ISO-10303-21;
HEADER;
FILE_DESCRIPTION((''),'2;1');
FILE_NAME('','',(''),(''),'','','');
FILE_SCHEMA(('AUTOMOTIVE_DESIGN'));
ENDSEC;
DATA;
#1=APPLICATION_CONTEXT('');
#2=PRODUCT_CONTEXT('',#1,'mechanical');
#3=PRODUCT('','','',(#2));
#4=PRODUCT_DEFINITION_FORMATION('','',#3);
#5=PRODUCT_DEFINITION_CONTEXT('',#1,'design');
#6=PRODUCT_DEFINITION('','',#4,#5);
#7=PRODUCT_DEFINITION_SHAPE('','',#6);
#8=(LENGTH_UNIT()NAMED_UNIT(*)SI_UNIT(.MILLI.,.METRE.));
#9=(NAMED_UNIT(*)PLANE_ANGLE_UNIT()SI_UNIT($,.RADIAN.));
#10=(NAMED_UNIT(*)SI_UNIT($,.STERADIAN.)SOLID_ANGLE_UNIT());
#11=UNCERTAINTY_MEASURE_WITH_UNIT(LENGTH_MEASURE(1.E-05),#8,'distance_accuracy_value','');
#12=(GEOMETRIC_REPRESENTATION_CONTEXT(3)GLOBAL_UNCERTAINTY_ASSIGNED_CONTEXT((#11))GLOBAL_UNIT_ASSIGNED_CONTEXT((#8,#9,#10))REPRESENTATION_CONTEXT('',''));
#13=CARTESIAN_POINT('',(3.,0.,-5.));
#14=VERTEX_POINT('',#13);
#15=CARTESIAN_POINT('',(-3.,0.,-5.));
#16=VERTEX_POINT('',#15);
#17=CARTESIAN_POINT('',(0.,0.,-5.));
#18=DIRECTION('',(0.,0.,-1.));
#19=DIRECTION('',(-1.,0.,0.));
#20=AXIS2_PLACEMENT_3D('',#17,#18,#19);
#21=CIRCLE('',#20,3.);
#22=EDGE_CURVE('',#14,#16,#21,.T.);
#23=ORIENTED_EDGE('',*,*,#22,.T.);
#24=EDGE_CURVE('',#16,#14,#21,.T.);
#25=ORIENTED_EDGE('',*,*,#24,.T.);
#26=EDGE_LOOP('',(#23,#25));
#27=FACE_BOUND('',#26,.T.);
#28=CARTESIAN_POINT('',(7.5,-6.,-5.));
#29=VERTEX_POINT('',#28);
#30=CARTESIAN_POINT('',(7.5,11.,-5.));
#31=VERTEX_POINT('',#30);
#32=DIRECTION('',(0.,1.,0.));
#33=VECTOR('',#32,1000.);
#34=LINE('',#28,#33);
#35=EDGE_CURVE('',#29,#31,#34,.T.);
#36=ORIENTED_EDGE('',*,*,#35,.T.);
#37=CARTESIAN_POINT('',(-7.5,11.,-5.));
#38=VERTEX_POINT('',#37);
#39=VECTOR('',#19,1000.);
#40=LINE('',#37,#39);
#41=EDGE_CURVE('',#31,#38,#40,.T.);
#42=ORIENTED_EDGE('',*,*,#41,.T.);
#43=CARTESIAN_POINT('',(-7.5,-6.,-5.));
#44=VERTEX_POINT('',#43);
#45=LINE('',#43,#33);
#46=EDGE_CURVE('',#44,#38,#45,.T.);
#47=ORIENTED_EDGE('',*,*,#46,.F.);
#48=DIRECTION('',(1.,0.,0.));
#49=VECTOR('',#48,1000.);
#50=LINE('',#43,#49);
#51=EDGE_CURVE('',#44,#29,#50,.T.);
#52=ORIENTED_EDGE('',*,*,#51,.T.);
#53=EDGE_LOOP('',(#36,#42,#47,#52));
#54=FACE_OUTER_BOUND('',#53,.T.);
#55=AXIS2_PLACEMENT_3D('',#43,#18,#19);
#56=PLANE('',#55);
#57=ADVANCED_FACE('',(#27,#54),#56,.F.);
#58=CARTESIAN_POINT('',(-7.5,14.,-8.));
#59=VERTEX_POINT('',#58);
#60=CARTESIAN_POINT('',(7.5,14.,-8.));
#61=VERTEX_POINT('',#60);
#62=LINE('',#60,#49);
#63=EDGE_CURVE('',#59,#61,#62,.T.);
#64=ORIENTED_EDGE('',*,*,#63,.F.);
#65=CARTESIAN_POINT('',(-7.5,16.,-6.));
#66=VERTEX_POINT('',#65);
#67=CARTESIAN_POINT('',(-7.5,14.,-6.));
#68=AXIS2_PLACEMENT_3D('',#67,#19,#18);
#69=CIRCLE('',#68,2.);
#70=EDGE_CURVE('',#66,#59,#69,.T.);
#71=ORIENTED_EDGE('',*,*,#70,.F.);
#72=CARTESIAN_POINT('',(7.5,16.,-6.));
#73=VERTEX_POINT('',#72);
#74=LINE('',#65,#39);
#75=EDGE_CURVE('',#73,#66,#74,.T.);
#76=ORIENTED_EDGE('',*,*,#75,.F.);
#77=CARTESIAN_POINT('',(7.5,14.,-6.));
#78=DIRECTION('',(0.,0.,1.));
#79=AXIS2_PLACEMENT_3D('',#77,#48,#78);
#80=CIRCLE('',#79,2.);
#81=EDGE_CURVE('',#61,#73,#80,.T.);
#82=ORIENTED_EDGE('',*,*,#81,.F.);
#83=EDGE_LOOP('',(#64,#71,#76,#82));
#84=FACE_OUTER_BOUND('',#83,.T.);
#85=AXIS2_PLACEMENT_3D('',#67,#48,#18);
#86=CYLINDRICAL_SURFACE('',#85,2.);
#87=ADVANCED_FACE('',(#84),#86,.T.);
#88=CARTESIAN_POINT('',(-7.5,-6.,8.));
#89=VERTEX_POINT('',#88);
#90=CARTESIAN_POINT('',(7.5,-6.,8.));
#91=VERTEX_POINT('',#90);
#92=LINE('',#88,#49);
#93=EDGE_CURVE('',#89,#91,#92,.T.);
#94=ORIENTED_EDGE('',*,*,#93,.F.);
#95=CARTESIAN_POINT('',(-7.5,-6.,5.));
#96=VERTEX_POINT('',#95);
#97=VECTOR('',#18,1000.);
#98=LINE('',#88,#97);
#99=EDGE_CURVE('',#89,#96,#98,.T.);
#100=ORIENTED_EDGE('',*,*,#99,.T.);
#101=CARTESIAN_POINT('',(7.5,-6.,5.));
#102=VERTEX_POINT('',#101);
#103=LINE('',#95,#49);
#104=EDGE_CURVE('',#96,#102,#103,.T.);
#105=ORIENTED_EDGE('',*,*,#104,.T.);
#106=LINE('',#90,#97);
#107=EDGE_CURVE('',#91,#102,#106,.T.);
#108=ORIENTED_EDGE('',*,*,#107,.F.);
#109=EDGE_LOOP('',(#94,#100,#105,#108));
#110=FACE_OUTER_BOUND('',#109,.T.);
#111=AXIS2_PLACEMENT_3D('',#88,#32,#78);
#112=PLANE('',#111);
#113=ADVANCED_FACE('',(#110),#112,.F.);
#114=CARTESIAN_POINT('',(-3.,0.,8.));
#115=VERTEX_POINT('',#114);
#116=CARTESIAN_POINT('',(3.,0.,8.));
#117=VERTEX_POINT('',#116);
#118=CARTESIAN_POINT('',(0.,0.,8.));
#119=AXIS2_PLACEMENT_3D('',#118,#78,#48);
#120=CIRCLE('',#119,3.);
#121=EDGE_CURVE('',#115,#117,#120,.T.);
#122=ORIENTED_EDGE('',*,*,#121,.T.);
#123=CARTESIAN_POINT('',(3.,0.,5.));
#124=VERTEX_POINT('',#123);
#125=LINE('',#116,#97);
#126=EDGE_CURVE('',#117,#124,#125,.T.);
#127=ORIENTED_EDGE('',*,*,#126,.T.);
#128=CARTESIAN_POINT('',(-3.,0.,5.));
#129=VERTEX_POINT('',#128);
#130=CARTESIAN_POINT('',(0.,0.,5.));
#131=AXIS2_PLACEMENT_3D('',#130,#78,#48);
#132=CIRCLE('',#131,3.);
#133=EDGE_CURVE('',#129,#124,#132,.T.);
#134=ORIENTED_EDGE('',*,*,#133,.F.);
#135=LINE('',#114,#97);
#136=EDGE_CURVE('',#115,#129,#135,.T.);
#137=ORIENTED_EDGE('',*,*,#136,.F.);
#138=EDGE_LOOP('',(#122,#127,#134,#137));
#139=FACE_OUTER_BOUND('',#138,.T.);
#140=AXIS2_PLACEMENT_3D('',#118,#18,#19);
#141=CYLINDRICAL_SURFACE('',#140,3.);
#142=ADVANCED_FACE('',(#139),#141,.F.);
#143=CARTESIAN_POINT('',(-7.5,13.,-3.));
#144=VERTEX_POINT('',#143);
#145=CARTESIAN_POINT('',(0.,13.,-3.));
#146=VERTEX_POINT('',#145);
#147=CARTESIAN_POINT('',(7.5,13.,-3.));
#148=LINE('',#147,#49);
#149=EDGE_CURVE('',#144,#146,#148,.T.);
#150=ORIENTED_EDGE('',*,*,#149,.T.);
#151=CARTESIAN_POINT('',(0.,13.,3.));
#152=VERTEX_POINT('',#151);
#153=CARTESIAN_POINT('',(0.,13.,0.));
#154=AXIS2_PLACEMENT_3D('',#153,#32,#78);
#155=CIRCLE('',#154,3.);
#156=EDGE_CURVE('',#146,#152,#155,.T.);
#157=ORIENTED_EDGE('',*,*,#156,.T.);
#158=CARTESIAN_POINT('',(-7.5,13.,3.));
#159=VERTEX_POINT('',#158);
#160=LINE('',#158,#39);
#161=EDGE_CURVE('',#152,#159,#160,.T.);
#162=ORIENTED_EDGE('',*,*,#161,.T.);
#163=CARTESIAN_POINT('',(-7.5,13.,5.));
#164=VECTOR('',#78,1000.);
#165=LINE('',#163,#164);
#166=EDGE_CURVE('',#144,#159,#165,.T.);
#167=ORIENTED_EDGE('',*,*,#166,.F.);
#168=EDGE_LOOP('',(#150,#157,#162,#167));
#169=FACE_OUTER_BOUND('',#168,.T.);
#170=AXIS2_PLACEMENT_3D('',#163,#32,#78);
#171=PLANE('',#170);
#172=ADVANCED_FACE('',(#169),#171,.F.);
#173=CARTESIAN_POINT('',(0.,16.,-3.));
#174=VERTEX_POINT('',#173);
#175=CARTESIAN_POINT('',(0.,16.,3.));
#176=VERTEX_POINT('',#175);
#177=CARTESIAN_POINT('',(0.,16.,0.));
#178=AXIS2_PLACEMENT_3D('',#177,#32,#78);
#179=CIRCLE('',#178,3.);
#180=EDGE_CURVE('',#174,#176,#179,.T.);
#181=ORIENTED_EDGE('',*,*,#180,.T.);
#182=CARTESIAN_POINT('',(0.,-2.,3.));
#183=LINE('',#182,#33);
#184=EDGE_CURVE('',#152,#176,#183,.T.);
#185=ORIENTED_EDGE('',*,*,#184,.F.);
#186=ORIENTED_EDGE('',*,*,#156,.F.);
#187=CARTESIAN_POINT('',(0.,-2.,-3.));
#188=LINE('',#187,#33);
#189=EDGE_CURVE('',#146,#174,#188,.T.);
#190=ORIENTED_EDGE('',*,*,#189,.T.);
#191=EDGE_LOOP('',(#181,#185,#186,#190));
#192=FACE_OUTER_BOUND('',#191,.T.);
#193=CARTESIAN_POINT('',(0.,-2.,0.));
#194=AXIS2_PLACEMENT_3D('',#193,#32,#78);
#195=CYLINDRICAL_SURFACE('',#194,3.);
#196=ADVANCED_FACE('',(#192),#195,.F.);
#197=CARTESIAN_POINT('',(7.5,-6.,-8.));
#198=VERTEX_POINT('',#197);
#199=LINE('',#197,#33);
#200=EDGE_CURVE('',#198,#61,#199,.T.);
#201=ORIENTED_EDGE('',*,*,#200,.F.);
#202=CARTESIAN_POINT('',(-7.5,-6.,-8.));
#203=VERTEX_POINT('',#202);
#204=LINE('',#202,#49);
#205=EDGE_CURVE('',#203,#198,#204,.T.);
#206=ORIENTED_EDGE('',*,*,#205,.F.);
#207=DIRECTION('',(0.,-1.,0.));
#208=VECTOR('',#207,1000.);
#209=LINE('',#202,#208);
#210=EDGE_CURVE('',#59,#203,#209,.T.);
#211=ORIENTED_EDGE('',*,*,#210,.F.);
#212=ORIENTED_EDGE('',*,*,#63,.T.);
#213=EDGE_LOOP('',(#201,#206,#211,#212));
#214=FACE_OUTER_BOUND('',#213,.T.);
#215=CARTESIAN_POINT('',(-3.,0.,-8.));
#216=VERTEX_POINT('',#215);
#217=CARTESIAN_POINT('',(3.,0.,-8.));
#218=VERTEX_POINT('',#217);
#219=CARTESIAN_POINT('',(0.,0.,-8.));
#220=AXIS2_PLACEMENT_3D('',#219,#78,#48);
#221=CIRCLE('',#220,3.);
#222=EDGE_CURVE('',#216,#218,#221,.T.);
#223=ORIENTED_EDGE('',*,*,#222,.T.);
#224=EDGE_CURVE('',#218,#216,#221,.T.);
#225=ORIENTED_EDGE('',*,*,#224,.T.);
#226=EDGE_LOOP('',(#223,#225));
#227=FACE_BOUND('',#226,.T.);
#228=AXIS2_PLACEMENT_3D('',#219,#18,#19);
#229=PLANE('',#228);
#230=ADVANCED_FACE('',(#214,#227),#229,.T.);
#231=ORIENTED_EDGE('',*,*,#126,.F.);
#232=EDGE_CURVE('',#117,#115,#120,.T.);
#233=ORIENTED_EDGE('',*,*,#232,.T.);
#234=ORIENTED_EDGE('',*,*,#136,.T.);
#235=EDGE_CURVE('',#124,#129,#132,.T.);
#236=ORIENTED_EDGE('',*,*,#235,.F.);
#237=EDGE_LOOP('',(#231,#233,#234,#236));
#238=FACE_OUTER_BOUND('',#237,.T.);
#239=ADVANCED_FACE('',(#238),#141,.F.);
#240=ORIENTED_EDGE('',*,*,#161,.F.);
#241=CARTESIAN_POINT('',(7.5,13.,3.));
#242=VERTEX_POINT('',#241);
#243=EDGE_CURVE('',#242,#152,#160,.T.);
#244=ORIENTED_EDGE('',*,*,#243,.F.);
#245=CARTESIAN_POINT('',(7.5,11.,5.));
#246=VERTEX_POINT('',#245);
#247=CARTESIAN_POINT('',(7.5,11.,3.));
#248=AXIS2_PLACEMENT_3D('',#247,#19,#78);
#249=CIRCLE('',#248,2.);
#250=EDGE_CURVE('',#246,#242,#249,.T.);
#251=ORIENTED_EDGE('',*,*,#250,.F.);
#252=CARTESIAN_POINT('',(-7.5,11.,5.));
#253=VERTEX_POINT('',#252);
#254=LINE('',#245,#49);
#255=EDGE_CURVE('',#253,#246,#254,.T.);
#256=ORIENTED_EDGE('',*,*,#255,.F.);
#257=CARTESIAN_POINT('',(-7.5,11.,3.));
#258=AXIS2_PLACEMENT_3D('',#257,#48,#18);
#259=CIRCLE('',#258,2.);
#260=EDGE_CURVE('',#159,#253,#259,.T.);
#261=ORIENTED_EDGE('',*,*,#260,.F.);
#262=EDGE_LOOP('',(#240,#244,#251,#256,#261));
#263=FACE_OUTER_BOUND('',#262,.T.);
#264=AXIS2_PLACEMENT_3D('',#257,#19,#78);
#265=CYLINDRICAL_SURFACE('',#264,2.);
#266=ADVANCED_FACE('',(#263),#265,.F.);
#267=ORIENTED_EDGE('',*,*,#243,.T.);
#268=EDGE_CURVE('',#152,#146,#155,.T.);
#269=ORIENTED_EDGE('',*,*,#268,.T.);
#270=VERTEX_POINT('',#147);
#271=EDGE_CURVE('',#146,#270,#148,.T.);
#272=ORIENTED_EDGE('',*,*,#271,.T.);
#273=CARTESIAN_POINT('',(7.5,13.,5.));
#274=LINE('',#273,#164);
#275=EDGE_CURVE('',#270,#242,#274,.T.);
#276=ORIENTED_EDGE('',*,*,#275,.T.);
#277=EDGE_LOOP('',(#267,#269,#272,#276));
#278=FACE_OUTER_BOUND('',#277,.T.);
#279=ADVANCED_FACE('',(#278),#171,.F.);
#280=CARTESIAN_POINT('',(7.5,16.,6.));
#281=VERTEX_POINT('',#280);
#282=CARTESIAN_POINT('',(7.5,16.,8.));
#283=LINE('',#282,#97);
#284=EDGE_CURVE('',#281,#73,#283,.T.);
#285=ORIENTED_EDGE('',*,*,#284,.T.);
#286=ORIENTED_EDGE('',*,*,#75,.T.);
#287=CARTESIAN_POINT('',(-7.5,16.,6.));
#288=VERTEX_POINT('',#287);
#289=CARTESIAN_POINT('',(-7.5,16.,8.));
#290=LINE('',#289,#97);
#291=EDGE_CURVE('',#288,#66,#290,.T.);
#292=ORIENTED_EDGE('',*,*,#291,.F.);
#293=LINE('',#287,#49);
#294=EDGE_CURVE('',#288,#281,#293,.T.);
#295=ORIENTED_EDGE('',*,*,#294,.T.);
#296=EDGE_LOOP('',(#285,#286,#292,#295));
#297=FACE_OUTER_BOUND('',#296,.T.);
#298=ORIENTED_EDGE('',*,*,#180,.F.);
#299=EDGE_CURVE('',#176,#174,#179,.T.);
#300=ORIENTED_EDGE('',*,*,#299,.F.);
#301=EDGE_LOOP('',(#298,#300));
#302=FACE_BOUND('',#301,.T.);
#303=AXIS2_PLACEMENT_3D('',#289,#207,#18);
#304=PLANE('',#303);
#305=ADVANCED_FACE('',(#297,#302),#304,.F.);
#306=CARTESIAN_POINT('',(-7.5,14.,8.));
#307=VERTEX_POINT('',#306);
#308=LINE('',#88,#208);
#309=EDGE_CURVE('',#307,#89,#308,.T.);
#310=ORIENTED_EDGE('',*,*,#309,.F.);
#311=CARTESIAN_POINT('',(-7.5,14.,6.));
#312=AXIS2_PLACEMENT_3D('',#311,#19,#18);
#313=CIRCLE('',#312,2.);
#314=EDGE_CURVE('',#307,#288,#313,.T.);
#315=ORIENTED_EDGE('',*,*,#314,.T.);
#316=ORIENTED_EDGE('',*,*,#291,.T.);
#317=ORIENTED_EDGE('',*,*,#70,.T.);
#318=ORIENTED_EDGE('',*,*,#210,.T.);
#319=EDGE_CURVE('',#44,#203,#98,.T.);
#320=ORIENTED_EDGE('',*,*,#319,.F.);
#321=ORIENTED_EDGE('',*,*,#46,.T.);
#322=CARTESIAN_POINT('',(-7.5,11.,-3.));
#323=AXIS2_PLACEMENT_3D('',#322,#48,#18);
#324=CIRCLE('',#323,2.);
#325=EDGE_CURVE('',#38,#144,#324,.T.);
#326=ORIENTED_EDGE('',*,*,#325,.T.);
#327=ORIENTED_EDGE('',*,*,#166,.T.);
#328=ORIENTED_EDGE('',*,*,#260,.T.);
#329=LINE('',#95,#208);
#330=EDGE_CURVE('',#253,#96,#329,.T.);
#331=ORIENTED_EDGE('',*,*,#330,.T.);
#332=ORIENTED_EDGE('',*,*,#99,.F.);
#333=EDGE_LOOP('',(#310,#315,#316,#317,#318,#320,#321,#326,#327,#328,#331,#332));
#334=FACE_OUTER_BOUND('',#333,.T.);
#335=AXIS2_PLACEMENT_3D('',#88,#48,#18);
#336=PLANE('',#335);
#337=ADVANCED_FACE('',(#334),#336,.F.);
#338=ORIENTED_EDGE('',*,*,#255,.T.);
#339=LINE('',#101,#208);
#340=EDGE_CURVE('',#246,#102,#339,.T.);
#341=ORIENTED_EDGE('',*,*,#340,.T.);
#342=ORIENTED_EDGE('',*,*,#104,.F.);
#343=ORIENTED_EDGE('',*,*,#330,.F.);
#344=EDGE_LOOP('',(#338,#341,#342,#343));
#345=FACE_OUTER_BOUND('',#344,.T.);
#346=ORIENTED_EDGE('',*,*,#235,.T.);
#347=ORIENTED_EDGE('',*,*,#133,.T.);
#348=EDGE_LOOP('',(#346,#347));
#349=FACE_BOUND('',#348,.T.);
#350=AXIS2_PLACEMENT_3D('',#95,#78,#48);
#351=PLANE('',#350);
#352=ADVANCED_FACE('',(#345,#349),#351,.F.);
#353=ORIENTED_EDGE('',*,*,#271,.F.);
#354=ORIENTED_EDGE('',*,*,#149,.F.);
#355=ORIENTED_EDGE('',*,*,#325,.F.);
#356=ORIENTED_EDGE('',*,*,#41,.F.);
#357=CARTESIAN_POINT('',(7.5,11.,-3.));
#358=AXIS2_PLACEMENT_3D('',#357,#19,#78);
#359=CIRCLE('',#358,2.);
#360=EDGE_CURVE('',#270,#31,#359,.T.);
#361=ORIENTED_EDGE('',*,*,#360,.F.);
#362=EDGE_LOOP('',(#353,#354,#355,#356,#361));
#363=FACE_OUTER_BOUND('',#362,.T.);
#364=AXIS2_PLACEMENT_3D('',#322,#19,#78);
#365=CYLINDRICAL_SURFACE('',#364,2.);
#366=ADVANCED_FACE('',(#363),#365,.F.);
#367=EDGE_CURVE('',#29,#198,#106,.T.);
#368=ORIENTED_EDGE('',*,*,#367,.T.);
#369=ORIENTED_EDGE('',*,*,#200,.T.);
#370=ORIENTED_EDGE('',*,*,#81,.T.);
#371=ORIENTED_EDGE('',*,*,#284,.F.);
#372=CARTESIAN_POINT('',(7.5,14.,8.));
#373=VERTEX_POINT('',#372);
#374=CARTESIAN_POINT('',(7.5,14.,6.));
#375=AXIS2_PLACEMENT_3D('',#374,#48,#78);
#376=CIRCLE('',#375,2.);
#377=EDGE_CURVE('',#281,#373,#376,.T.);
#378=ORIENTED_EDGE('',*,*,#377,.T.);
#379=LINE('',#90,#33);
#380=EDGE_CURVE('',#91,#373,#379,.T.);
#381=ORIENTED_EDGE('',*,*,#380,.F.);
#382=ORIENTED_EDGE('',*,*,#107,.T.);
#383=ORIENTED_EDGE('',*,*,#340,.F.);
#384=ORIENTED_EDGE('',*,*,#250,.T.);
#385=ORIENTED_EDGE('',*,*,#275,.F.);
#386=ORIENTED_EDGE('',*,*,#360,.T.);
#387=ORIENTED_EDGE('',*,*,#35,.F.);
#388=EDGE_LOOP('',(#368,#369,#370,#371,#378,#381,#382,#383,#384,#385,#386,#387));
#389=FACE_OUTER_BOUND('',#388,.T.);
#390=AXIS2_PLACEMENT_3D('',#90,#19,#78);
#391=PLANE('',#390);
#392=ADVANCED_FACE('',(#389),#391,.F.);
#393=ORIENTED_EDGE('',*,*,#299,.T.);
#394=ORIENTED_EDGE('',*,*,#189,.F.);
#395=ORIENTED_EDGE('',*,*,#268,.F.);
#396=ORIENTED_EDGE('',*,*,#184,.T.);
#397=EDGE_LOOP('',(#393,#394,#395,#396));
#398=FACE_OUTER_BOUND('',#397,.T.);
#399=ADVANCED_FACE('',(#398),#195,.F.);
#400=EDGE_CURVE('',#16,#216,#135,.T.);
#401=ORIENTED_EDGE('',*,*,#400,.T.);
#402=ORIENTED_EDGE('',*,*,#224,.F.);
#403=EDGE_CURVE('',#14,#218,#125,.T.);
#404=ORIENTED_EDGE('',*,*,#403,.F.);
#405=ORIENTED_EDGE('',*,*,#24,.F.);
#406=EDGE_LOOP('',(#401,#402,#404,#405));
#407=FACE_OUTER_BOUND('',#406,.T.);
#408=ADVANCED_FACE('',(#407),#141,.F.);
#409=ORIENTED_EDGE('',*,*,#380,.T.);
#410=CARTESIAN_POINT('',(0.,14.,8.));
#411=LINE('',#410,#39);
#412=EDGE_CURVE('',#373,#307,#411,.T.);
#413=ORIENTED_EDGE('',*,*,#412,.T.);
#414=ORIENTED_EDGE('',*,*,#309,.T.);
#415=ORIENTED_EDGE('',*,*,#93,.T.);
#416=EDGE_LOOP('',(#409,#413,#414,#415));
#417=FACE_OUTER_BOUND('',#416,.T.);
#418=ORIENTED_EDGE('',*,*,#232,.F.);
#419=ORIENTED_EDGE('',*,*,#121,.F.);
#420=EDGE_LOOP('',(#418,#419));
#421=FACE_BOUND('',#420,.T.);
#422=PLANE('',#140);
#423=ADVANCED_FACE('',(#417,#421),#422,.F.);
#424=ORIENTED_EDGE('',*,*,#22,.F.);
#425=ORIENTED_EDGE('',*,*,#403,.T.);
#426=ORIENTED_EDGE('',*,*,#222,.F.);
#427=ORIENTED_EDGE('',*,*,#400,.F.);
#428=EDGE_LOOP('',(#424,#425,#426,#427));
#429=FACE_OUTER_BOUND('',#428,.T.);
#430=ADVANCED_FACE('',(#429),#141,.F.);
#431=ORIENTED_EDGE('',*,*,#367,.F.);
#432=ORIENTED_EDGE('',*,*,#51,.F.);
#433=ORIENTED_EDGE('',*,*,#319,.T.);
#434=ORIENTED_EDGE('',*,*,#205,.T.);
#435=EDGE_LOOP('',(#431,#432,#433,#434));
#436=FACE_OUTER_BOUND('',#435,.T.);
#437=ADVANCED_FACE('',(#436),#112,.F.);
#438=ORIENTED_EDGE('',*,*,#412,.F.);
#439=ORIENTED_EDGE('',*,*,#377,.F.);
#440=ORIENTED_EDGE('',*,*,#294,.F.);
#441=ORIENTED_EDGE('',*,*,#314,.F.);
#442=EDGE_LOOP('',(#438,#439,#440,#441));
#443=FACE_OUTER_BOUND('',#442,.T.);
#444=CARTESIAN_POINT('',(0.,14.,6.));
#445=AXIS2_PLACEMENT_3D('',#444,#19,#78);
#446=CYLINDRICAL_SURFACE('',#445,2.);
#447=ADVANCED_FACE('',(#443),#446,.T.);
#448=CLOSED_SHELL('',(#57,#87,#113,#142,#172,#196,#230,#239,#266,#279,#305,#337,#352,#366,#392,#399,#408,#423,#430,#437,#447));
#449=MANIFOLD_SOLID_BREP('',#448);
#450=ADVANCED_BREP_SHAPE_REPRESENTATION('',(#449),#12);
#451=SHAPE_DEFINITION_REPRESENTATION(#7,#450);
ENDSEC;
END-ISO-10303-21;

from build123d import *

# Parameters (mm, degrees)
SKETCH1_W           = 15
SKETCH1_H           = 22
SKETCH1_R           = 3
BOSS_EXTRUDE1_DEPTH = 8
SKETCH2_W           = 10
SKETCH2_H           = 19
CUT_EXTRUDE1_DEPTH  = 24.34523506
FILLET1_R           = 2
SKETCH3_R           = 3
CUT_EXTRUDE2_DEPTH  = 18


with BuildPart() as part:
    # Sketch1 → Boss-Extrude1 (new, symmetric)
    with BuildSketch(Plane.XY):
        with Locations((0, 5)):
            Rectangle(SKETCH1_W, SKETCH1_H)
        Circle(SKETCH1_R, mode=Mode.SUBTRACT)
    extrude(amount=BOSS_EXTRUDE1_DEPTH, both=True)

    # Sketch2 → Cut-Extrude1 (cut, through all)
    with BuildSketch(Plane(origin=(7.5, 0, 0), x_dir=(0, 0, -1), z_dir=(1, 0, 0))):
        with Locations((0, 3.5)):
            Rectangle(SKETCH2_W, SKETCH2_H)
    extrude(amount=-CUT_EXTRUDE1_DEPTH, mode=Mode.SUBTRACT)

    # Fillet1
    fillet1_edges = [part.edges().sort_by_distance(p)[0] for p in [
        (0, 16, 8),
        (0, 13, 5),
        (0, 13, -5),
        (0, 16, -8),
    ]]
    fillet(fillet1_edges, radius=FILLET1_R)

    # Sketch3 → Cut-Extrude2 (cut)
    with BuildSketch(Plane(origin=(0, 16, 0), x_dir=(1, 0, 0), z_dir=(0, 1, 0))):
        with Locations(Location((0, 0, 0), (0, 0, 270))):
            Circle(SKETCH3_R)
    extrude(amount=-CUT_EXTRUDE2_DEPTH, mode=Mode.SUBTRACT)


solid = part.part
